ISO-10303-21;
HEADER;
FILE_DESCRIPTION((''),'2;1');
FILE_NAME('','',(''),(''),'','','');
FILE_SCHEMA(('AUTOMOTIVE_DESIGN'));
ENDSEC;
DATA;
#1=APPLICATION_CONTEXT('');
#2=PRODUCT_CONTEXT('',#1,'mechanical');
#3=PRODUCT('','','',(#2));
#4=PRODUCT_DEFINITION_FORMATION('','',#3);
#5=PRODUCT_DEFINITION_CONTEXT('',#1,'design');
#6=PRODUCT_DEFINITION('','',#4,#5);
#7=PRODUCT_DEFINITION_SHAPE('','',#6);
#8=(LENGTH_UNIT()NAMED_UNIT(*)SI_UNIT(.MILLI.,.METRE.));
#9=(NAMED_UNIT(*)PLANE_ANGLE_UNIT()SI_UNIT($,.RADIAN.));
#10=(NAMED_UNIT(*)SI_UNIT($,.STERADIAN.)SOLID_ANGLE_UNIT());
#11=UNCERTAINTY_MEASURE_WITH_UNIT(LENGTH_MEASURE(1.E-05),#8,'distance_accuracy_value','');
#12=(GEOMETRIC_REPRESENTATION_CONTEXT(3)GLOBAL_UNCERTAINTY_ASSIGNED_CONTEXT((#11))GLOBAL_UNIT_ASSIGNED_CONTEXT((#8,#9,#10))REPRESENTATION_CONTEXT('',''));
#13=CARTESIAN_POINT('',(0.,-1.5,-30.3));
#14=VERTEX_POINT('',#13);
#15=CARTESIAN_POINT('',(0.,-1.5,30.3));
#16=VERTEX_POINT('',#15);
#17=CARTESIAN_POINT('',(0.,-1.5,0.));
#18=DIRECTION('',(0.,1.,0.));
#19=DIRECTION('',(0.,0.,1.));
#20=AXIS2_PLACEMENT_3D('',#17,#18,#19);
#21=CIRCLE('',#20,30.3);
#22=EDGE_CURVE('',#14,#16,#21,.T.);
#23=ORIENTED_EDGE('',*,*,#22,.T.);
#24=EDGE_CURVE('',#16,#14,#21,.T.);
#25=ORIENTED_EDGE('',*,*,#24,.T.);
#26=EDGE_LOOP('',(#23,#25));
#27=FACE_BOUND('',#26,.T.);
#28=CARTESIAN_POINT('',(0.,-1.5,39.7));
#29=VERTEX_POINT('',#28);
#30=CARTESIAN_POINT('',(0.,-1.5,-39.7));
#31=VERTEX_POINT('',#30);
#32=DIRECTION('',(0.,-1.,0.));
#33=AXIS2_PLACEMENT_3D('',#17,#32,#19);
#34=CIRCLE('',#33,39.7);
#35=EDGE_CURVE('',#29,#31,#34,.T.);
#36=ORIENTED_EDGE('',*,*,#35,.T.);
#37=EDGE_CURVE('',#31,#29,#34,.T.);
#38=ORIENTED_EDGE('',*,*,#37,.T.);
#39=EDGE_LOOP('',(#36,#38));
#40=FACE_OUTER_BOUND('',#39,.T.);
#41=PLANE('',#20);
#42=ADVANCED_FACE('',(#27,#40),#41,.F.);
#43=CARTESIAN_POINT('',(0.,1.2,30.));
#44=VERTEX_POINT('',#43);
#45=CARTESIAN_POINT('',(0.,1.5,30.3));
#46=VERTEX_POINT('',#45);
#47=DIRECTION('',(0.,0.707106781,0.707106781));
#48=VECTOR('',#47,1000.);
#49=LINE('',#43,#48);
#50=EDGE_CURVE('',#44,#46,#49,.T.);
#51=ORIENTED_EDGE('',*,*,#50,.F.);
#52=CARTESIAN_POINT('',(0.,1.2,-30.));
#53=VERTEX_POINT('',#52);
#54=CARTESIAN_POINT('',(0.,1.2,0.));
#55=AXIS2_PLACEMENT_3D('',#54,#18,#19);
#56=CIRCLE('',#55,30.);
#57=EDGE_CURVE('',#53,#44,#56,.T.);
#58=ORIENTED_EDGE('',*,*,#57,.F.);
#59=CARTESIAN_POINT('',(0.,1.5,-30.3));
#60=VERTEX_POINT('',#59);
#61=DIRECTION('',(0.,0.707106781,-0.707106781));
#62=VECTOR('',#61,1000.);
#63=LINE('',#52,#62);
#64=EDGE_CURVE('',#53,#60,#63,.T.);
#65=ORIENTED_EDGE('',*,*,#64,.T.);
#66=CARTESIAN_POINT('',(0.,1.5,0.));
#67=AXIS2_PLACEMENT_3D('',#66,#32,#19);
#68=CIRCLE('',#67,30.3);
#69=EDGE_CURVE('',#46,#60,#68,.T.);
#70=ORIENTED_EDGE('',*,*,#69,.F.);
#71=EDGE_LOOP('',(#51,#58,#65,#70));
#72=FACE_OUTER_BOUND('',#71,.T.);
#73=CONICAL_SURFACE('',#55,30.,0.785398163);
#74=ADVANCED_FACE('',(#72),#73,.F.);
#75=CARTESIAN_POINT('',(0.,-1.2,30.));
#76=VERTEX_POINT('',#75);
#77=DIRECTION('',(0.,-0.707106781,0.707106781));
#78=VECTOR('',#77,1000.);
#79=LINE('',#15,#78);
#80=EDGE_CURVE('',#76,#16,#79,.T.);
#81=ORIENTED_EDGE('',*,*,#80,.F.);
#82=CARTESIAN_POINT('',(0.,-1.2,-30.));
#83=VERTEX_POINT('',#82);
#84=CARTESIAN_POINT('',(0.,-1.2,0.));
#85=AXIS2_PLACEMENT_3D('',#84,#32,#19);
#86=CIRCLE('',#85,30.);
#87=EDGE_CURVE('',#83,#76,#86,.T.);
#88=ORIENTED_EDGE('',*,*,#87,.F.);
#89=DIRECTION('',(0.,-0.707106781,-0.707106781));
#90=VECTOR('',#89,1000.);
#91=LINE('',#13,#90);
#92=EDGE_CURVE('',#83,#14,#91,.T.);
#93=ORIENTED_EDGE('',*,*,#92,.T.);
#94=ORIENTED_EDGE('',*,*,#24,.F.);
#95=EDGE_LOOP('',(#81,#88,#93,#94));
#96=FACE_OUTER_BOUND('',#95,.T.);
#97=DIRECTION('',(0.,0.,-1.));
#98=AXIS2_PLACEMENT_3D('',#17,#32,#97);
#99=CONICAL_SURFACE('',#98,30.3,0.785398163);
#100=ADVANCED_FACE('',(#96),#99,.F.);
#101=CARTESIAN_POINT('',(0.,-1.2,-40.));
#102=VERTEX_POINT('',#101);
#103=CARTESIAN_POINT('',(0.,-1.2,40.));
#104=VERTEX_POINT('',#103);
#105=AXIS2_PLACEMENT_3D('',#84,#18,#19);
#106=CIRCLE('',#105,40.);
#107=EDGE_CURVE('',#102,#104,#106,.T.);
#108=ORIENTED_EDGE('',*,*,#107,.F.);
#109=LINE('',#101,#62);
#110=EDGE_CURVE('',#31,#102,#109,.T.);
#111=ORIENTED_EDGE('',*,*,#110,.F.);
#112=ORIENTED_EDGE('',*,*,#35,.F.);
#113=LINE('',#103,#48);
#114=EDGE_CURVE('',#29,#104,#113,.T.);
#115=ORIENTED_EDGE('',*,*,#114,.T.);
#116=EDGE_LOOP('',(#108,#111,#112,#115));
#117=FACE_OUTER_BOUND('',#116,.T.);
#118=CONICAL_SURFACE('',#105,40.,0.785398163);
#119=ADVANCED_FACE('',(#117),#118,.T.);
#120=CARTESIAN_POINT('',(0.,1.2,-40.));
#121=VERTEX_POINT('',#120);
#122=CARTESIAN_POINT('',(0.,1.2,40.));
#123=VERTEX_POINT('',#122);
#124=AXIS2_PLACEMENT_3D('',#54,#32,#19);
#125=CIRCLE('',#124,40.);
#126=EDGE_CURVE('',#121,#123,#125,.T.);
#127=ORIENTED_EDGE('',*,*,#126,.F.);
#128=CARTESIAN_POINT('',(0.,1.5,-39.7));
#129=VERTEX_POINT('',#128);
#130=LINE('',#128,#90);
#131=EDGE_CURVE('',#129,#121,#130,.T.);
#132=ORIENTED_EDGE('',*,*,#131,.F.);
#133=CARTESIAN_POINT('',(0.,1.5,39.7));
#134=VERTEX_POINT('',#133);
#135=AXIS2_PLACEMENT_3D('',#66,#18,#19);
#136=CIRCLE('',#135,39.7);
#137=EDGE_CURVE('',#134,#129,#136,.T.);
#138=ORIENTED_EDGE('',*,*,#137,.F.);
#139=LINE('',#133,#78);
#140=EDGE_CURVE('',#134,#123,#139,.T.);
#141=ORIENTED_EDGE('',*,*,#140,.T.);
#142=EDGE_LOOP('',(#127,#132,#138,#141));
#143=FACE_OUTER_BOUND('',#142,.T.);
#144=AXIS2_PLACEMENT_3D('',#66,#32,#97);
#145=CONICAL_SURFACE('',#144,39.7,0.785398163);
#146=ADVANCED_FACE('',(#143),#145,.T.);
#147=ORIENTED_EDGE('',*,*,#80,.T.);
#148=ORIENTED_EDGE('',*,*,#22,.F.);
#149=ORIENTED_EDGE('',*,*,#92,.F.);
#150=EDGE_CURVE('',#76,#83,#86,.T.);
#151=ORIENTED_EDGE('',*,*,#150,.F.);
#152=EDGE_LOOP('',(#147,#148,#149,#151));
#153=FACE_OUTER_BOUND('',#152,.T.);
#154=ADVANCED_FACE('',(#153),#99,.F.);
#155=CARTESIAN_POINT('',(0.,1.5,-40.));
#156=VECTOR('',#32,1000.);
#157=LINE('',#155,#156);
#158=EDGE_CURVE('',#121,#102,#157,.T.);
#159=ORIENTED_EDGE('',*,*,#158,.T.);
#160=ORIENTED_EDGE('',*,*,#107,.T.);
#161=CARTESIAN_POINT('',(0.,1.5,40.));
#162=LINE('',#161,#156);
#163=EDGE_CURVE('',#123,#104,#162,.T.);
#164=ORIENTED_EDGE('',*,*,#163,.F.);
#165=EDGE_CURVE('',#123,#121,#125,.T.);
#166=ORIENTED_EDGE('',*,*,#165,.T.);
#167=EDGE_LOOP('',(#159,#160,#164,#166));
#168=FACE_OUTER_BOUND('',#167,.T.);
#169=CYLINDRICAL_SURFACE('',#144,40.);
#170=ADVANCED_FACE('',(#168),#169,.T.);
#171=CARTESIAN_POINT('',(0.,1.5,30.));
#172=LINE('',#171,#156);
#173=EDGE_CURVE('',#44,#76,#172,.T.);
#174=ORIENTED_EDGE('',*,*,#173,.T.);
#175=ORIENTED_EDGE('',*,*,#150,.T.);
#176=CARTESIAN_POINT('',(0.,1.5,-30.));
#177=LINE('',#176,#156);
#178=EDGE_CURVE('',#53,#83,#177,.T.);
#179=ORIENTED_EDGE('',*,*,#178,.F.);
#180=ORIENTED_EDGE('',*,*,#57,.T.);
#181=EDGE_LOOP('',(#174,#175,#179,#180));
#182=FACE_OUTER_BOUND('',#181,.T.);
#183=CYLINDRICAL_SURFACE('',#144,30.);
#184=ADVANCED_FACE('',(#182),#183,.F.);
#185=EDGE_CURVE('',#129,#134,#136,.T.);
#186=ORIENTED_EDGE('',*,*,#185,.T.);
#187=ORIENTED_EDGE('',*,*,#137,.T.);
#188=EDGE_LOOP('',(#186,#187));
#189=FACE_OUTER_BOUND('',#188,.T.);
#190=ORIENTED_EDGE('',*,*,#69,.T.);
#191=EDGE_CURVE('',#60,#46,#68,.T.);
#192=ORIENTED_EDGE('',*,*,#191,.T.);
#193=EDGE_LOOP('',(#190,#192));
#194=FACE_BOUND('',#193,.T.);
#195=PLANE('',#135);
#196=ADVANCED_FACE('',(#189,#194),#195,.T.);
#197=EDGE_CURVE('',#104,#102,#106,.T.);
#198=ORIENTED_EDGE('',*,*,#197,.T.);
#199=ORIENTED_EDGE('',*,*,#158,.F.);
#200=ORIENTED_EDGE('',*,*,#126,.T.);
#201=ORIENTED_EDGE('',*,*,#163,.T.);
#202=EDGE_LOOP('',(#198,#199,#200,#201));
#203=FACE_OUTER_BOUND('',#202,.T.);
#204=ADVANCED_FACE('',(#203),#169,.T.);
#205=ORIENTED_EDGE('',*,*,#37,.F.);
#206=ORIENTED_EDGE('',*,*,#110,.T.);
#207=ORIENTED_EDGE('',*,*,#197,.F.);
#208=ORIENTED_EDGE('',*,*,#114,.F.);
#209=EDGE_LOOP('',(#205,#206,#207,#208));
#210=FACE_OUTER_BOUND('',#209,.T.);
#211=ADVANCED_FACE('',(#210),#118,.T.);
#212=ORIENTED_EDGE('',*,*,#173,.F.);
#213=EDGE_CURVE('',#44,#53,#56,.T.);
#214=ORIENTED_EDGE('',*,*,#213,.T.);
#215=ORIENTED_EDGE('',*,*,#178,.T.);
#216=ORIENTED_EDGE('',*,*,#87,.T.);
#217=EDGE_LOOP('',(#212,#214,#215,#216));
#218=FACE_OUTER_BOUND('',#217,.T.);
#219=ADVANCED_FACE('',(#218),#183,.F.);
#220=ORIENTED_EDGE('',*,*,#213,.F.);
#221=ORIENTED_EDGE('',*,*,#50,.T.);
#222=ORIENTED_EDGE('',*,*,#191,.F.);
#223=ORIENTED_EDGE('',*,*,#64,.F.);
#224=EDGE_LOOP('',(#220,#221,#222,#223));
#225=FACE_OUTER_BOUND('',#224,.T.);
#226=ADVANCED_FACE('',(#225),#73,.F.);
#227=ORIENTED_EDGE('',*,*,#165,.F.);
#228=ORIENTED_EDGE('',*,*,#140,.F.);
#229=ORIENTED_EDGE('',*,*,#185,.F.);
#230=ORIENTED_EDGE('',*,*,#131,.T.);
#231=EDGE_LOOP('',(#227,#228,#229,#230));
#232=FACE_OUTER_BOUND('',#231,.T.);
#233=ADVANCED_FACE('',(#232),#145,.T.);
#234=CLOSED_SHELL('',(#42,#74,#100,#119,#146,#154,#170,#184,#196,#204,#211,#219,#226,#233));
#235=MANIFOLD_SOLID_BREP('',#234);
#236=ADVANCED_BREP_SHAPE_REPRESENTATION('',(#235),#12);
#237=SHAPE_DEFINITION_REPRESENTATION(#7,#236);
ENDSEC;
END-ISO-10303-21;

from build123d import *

# Parameters (mm, degrees)
SKETCH1_R           = 40
SKETCH1_R_2         = 30
BOSS_EXTRUDE1_DEPTH = 1.5
CHAMFER1_SIZE       = 0.3


with BuildPart() as part:
    # Sketch1 → Boss-Extrude1 (new, symmetric)
    with BuildSketch(Plane(origin=(0, 0, 0), x_dir=(1, 0, 0), z_dir=(0, 1, 0))):
        with Locations(Location((0, 0, 0), (0, 0, 270))):
            Circle(SKETCH1_R)
        with Locations(Location((0, 0, 0), (0, 0, 270))):
            Circle(SKETCH1_R_2, mode=Mode.SUBTRACT)
    extrude(amount=BOSS_EXTRUDE1_DEPTH, both=True)

    # Chamfer1
    chamfer1_edges = [part.edges().sort_by_distance(p)[0] for p in [
        (0, -1.5, -40),
        (0, 1.5, -40),
        (0, -1.5, -30),
        (0, 1.5, -30),
    ]]
    chamfer(chamfer1_edges, length=CHAMFER1_SIZE)


solid = part.part
